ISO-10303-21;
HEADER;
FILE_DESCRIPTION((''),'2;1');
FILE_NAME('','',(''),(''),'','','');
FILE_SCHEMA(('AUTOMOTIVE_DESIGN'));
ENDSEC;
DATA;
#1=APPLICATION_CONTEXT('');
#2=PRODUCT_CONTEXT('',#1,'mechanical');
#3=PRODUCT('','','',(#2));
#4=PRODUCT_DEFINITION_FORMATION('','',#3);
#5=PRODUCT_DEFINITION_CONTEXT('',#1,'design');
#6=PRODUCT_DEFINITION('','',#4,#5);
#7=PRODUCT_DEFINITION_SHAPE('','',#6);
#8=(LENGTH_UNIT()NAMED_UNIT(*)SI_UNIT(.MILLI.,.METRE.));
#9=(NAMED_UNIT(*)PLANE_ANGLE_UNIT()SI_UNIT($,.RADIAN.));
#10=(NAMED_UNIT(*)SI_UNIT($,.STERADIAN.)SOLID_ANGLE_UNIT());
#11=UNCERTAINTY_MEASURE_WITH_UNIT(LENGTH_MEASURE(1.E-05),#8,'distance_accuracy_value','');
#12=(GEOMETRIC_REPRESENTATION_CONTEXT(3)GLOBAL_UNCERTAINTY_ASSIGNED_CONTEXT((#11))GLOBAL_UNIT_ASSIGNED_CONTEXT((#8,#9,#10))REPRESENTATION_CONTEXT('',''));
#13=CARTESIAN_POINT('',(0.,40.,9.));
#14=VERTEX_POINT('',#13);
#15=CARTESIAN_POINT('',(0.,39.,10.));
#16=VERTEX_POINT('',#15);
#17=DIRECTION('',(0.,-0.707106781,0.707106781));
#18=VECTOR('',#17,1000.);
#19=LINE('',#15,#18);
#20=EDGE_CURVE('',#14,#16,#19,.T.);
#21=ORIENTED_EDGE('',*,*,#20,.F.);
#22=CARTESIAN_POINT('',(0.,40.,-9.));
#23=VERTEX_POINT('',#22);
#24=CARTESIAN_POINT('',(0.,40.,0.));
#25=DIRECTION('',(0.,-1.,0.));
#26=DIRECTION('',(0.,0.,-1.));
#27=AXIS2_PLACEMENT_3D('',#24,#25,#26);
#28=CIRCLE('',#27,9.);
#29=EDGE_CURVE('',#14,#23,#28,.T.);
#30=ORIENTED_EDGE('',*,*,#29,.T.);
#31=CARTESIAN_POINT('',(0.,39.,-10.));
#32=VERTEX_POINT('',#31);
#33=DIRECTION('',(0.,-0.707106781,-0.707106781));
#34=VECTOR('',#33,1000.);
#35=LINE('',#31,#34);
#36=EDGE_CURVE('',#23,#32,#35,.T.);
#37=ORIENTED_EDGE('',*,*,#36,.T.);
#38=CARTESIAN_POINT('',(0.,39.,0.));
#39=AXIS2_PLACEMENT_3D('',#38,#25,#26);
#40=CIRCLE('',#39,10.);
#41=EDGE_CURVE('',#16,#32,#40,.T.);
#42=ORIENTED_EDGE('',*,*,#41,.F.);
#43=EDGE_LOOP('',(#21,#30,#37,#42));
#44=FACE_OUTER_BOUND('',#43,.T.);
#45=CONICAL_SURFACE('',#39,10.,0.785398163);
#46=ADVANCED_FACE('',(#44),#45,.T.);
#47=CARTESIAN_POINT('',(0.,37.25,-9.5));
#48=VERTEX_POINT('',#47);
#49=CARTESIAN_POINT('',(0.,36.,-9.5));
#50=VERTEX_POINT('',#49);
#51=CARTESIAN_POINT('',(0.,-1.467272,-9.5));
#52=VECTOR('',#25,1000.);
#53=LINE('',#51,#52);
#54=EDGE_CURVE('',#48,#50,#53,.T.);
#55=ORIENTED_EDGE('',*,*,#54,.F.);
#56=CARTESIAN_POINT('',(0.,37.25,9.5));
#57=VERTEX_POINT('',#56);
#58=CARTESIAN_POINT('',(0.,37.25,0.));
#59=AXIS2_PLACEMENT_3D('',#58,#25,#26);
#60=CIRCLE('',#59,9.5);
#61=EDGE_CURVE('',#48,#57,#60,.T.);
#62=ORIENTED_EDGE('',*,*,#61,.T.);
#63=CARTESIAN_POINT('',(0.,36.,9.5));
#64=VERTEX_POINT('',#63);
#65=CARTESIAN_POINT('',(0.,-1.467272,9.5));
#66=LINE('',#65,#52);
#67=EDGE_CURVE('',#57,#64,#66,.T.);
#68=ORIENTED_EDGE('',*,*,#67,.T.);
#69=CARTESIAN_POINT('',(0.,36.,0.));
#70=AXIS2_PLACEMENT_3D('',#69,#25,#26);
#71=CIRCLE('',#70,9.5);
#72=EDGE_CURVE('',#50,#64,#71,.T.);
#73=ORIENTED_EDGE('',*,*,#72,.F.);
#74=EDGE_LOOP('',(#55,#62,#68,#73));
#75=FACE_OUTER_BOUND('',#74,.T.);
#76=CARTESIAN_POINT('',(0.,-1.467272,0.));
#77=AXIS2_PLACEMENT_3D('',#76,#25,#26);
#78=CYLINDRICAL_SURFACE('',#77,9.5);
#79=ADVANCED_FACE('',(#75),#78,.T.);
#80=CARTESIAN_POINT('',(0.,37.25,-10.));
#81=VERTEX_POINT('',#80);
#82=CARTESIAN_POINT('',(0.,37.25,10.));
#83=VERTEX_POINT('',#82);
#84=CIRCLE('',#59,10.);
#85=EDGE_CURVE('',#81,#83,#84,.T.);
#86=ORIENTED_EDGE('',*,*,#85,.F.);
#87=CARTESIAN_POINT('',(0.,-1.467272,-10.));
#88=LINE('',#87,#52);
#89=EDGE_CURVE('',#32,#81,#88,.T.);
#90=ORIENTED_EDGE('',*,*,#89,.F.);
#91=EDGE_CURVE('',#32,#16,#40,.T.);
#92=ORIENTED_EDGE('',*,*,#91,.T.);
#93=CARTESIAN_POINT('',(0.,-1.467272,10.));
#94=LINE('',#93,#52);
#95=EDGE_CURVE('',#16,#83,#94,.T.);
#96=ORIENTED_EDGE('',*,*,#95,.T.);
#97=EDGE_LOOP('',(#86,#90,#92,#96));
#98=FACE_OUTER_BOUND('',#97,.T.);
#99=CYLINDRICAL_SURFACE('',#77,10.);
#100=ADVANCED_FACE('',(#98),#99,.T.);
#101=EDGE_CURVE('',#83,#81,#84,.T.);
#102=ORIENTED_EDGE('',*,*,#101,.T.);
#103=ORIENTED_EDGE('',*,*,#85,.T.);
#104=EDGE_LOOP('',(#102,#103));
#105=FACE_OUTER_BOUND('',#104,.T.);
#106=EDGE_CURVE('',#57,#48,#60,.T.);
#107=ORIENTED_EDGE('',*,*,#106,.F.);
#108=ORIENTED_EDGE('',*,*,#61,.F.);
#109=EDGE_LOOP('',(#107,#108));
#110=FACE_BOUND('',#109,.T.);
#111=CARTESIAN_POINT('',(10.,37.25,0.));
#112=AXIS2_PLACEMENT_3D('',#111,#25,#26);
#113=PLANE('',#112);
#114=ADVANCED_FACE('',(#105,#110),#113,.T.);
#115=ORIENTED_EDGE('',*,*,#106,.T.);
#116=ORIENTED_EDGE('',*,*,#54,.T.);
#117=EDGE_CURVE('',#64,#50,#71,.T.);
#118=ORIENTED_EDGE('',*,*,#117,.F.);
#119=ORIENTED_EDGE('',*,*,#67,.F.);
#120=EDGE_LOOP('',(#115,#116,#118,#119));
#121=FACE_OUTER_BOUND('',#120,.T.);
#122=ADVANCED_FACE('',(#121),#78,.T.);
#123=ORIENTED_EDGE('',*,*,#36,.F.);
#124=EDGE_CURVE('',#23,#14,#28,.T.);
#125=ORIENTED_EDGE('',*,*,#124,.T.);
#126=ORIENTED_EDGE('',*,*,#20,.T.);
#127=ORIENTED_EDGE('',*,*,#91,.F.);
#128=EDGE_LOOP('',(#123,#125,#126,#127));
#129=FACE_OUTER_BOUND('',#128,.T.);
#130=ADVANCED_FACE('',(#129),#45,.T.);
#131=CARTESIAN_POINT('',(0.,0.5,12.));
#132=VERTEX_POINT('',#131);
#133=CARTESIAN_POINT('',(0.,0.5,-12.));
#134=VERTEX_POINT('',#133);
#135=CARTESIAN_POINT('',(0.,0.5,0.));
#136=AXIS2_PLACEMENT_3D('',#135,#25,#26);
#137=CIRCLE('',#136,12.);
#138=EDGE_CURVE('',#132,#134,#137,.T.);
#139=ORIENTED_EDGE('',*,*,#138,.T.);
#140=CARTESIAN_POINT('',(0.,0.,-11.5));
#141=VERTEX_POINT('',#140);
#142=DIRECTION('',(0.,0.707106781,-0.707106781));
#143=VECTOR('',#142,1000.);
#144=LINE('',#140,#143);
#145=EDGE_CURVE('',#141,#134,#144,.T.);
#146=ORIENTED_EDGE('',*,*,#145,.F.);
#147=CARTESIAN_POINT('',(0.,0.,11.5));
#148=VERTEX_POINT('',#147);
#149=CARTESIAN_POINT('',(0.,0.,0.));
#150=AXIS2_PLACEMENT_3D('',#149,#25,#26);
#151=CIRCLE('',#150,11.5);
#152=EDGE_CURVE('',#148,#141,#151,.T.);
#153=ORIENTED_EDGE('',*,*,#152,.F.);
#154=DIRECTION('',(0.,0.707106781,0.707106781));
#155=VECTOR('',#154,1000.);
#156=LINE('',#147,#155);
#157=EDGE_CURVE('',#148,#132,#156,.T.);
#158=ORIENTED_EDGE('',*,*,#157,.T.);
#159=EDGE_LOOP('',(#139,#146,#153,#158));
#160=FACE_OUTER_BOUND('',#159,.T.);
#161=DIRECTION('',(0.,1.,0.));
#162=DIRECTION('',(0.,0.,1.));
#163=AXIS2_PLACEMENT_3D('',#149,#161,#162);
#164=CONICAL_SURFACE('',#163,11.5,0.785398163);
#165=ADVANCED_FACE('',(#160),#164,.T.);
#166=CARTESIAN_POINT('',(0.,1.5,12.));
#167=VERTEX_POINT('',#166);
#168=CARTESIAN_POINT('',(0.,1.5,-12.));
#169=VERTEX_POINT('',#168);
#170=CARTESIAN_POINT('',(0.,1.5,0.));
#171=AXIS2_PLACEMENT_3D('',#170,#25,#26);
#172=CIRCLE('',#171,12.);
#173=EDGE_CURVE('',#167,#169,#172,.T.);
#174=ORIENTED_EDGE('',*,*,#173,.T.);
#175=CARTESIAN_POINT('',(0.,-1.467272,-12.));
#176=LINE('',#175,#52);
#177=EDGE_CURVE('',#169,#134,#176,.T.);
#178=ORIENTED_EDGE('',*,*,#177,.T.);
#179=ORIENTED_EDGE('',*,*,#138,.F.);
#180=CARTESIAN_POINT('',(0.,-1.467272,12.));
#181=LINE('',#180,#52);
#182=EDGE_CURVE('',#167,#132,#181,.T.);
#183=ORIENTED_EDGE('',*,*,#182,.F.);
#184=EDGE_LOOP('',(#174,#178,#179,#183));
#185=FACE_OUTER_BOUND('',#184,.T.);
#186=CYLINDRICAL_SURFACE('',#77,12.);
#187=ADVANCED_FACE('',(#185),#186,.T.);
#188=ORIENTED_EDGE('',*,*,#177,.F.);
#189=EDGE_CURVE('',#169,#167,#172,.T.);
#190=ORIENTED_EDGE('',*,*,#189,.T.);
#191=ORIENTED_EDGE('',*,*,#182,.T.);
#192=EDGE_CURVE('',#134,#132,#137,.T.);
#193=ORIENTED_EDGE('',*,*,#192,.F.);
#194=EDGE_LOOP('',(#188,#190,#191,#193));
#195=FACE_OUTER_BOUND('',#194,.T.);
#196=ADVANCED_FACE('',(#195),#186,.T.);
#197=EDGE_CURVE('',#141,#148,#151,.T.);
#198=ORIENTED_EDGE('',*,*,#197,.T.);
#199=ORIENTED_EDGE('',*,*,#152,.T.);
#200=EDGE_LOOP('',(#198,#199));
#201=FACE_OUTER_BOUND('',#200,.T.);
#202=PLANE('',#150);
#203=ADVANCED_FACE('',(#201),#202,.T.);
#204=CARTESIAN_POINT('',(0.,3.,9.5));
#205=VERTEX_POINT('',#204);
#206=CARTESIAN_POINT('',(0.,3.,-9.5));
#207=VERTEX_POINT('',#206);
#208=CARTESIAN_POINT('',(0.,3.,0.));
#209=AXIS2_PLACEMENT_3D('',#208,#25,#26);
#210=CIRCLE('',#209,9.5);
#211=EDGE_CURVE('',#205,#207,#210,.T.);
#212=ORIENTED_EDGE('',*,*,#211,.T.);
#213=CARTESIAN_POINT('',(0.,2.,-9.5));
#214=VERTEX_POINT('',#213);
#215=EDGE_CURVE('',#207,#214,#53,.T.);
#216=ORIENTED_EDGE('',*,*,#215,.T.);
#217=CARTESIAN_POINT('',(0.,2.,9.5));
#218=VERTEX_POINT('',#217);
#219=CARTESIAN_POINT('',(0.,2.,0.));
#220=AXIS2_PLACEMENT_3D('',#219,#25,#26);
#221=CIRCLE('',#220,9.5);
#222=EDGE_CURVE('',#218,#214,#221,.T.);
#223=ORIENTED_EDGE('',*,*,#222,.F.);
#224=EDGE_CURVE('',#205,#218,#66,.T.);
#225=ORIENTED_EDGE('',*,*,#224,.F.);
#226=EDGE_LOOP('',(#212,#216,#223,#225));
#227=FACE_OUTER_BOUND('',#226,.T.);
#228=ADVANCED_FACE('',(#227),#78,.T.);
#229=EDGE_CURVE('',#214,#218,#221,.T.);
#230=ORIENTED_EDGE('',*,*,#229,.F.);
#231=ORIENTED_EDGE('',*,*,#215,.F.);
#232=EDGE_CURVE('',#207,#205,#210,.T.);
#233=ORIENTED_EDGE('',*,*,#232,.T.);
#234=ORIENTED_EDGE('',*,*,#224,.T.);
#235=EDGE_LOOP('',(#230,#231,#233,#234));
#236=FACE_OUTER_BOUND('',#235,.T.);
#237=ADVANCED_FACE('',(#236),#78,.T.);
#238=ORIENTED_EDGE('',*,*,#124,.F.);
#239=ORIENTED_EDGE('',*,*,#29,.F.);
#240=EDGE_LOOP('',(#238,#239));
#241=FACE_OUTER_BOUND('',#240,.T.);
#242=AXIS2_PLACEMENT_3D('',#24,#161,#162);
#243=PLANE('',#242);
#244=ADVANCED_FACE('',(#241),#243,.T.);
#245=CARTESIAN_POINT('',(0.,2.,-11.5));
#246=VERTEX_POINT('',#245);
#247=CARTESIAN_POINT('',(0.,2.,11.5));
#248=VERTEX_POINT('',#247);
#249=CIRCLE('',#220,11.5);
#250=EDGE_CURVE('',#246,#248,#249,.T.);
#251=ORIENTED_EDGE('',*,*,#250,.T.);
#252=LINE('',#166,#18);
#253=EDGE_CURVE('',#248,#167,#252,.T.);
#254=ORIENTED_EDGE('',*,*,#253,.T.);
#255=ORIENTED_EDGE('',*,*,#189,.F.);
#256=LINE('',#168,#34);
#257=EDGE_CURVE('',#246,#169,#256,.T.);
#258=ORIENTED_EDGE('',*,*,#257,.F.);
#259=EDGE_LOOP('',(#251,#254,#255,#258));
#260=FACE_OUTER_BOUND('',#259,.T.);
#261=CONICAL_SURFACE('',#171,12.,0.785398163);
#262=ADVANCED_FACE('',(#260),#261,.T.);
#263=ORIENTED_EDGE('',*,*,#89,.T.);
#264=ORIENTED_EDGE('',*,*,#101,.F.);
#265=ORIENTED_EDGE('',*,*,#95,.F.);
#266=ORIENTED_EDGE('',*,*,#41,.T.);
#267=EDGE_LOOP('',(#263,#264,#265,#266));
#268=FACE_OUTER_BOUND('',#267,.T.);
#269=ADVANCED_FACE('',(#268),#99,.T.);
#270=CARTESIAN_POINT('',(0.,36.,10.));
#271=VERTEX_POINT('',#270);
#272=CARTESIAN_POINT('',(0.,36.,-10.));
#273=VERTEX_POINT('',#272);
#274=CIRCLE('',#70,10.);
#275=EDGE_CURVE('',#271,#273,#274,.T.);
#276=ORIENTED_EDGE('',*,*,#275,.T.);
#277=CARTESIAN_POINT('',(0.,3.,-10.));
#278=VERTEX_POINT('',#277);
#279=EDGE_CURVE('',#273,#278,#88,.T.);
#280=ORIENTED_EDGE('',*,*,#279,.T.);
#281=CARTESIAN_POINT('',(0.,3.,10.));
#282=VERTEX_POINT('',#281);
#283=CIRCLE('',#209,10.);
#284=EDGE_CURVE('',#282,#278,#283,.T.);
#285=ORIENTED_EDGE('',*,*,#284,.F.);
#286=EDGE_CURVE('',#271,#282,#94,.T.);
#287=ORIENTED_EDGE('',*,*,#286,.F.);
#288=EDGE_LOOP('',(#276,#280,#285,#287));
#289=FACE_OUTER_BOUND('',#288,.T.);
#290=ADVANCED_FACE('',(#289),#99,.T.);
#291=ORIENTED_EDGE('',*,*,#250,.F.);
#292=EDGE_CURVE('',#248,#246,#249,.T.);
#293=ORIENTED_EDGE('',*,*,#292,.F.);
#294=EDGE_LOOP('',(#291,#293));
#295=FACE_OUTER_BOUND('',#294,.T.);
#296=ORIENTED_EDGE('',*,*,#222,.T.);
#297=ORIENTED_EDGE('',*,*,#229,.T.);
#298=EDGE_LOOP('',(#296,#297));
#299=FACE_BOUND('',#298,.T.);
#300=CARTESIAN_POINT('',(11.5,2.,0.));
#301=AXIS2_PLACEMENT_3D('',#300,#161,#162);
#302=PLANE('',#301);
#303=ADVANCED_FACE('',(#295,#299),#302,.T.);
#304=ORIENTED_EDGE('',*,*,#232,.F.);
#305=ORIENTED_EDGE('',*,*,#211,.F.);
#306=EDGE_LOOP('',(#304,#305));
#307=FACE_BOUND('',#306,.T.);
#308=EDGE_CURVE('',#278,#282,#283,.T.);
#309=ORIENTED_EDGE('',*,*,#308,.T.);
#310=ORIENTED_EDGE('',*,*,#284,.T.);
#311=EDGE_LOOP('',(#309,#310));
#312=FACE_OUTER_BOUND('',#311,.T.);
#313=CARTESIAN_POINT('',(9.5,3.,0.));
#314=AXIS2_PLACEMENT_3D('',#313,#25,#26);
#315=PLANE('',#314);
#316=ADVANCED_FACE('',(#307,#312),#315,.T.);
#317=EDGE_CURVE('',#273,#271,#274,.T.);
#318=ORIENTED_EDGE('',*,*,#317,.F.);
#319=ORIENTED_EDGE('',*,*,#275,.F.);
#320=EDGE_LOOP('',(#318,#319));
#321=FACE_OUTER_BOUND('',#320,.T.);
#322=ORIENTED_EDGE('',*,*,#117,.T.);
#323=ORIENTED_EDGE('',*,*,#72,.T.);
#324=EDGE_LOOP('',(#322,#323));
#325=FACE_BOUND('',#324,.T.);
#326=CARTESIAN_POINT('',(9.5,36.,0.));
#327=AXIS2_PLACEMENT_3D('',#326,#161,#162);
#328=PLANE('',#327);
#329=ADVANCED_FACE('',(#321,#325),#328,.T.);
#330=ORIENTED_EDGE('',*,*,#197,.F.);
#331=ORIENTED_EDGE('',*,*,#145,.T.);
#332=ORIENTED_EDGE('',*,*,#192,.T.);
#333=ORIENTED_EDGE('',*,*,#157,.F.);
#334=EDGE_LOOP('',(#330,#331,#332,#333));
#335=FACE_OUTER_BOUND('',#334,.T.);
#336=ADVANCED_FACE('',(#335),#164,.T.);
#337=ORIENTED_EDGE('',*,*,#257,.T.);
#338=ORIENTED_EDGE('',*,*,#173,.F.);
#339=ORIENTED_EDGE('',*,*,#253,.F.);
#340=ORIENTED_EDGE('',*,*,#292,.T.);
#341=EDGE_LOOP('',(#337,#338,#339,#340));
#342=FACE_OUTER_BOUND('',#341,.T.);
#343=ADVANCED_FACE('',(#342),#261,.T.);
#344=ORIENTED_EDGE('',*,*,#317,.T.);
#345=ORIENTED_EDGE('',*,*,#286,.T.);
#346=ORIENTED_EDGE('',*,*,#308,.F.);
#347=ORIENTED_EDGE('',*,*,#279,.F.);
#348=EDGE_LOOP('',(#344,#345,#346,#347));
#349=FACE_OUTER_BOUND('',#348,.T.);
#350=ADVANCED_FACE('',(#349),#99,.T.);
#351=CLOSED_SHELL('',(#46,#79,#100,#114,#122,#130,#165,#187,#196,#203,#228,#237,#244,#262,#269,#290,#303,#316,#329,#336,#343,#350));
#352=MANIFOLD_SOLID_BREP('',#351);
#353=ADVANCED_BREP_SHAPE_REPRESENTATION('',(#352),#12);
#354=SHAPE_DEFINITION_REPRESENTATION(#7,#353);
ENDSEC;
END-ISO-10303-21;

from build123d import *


with BuildPart() as part:
    # 草图1 → 旋转1 (revolve)
    with BuildSketch(Plane.XY, mode=Mode.PRIVATE) as revolve_1_sk:
        Polygon((11.5, 2), (9.5, 2), (9.5, 3), (10, 3), (10, 36), (9.5, 36), (9.5, 37.25), (10, 37.25), (10, 39), (9, 40), (0, 40), (0, 0), (11.5, 0), (12, 0.5), (12, 1.5), align=None)
    revolve(revolve_1_sk.sketch.rotate(Axis((0, -1.467272455, 0), (0, 1, 0)), 90), axis=Axis((0, -1.467272455, 0), (0, 1, 0)))


solid = part.part
